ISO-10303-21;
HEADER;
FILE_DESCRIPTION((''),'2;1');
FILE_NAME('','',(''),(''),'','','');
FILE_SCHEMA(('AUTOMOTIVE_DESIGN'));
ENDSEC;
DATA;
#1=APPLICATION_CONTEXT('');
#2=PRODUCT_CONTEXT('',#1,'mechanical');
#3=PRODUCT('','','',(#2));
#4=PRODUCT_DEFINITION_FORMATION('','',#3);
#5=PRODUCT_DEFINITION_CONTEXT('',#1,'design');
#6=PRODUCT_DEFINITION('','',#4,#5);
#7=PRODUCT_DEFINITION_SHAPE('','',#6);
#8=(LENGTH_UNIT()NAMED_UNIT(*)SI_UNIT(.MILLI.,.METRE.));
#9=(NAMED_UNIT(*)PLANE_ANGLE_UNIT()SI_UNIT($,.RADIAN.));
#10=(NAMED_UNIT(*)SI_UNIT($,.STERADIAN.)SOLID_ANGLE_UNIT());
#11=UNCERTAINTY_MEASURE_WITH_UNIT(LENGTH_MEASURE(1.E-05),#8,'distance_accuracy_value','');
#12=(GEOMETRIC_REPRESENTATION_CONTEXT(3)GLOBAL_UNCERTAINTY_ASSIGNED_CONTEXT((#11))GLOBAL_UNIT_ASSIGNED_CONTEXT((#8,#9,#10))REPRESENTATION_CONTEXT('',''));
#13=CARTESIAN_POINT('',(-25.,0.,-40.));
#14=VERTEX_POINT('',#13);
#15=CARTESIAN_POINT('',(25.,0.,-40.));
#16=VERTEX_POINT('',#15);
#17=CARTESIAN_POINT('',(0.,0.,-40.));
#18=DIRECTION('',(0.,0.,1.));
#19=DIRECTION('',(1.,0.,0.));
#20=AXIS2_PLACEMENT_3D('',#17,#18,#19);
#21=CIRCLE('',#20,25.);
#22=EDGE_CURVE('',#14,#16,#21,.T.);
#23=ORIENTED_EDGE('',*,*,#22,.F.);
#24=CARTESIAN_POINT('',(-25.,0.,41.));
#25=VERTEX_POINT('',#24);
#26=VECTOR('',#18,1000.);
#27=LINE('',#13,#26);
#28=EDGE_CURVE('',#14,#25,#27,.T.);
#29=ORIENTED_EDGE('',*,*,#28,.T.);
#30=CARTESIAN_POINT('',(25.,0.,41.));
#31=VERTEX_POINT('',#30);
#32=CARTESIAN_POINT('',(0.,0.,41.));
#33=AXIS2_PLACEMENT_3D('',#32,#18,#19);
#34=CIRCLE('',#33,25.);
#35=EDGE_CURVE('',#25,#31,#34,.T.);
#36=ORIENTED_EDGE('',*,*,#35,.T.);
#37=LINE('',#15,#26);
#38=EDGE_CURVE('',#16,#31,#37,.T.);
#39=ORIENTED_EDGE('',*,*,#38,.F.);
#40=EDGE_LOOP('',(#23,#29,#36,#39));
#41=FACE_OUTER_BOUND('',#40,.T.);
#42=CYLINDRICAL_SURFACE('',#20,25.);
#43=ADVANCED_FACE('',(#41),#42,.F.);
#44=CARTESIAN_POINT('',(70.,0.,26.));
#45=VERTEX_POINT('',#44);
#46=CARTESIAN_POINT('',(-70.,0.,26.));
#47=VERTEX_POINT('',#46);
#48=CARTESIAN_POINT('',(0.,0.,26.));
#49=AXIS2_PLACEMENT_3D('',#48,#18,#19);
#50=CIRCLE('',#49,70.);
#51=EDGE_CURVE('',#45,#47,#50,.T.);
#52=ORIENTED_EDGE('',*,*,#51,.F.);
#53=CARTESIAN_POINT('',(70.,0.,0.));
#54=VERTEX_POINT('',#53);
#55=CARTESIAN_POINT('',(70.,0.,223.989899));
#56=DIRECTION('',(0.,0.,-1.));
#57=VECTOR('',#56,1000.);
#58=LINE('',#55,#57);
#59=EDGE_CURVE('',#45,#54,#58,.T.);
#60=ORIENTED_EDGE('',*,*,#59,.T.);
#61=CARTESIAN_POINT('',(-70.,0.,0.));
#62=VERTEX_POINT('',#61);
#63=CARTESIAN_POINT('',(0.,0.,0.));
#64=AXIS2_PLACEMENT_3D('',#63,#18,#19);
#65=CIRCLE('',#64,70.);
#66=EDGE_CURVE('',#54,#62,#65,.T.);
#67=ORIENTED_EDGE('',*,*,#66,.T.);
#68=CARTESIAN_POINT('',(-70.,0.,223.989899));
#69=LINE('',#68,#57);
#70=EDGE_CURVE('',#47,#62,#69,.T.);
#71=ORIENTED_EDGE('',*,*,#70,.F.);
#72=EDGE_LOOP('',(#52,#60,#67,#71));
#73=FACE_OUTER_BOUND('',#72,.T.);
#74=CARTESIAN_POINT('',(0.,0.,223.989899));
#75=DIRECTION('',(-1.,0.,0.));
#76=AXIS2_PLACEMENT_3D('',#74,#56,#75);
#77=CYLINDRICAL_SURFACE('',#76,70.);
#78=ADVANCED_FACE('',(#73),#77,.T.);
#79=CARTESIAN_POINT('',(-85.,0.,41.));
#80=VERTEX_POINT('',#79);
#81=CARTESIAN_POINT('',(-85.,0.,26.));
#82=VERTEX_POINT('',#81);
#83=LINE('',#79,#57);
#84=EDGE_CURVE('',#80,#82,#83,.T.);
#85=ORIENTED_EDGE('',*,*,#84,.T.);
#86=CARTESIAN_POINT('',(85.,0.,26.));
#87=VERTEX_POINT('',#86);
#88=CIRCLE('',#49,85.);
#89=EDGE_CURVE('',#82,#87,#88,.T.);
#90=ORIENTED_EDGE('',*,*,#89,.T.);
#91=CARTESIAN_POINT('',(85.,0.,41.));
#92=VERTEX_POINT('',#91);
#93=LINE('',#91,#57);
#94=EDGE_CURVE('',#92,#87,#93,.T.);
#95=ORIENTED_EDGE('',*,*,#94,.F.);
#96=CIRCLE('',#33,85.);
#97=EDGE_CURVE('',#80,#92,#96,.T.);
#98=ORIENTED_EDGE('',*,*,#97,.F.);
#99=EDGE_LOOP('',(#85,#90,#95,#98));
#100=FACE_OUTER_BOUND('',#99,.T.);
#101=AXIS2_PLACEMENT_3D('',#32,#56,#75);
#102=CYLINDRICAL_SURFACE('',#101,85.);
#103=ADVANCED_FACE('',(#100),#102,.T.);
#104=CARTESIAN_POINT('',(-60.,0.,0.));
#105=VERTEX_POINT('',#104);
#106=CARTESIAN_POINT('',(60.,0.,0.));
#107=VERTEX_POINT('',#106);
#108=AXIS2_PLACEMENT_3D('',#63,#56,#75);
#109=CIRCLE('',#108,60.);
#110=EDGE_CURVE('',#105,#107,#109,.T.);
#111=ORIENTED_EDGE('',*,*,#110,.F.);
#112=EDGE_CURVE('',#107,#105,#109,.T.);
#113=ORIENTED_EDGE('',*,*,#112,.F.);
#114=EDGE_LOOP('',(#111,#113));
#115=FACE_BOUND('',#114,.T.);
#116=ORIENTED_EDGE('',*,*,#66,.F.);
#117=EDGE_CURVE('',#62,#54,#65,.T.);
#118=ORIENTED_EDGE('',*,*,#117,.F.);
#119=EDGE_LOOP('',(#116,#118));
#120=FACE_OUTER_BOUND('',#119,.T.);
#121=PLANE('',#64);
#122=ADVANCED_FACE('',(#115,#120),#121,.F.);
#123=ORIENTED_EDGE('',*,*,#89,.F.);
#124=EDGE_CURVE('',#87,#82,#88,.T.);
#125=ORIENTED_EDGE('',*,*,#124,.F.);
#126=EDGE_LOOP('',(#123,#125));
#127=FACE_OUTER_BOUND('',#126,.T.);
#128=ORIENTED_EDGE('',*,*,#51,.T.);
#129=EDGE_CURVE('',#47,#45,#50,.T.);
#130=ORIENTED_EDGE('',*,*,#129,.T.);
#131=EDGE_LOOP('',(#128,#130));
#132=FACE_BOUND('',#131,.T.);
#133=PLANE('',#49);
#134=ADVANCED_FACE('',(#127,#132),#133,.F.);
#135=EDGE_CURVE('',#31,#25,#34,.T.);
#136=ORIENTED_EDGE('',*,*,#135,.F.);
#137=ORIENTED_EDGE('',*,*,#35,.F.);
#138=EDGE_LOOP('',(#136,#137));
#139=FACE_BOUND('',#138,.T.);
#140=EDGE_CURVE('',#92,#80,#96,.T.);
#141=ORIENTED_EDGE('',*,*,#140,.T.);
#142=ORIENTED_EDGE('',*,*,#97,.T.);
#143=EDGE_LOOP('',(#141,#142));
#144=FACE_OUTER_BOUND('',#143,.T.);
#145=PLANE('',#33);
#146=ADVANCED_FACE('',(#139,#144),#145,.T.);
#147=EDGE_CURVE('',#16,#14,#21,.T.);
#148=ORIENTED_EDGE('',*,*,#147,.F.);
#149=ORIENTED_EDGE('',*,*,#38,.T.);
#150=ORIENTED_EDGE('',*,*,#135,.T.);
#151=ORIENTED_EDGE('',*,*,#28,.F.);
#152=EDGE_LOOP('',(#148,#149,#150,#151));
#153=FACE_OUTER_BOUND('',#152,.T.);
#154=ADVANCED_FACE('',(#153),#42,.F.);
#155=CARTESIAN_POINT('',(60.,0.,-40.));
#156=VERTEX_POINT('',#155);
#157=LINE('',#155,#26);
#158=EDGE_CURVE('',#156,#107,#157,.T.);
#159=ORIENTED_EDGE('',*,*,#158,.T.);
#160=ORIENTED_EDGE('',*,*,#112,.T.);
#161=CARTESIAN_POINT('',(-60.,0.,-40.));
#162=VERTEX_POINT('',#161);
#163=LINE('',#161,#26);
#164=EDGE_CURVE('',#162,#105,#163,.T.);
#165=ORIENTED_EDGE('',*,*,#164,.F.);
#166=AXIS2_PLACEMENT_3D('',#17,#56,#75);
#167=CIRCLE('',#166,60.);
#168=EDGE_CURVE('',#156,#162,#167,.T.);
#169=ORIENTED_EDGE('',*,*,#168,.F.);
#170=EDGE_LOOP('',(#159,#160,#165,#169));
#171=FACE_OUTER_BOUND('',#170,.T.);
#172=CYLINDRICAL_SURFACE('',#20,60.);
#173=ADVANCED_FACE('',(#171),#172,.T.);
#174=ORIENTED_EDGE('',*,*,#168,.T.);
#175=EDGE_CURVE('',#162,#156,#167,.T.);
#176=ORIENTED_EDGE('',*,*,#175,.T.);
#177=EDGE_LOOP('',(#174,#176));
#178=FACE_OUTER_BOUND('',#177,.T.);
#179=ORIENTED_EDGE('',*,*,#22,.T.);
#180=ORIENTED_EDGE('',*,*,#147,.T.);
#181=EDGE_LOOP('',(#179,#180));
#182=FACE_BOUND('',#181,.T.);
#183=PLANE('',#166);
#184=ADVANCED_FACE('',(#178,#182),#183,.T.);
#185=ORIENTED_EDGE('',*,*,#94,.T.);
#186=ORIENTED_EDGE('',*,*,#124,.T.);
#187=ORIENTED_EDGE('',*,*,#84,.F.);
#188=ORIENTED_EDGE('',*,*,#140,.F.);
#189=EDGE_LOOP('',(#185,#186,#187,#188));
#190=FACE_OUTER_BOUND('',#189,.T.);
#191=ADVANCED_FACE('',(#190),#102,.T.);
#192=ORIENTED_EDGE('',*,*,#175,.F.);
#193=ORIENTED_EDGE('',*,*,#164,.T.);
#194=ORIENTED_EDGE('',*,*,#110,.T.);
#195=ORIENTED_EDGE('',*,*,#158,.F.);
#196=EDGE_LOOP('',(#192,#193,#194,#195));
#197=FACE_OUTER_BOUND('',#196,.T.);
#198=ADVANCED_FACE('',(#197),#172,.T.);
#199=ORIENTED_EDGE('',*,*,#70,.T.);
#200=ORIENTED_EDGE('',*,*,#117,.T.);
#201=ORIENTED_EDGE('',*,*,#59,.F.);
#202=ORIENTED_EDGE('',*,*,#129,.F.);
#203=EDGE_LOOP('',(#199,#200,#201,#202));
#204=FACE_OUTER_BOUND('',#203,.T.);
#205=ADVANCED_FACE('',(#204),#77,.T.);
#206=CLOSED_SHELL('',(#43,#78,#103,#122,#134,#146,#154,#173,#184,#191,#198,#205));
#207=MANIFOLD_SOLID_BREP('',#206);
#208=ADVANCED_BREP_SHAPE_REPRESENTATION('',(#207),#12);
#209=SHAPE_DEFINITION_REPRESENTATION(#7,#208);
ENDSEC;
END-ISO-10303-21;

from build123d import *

# Parameters (mm, degrees)
SKETCH1_R               = 70
BOSS_EXTRUDE1_DEPTH     = 26
SKETCH2_R               = 85
BOSS_EXTRUDE2_DEPTH     = 15
SKETCH3_R               = 60
BOSS_EXTRUDE3_DEPTH     = 40
CUT_EXTRUDE1_DEPTH      = 145.951716099
CUT_EXTRUDE1_DEPTH_BACK = 145.951716099
SKETCH4_R               = 25


with BuildPart() as part:
    # Sketch1 → Boss-Extrude1 (new body)
    with BuildSketch(Plane.XY):
        Circle(SKETCH1_R)
    extrude(amount=BOSS_EXTRUDE1_DEPTH)

    # Sketch2 → Boss-Extrude2 (add)
    with BuildSketch(Plane.XY.offset(26)):
        Circle(SKETCH2_R)
    extrude(amount=BOSS_EXTRUDE2_DEPTH)

    # Sketch3 → Boss-Extrude3 (add)
    with BuildSketch(Plane(origin=(0, 0, 0), x_dir=(-1, 0, 0), z_dir=(0, 0, -1))):
        Circle(SKETCH3_R)
    extrude(amount=BOSS_EXTRUDE3_DEPTH)

    # Sketch4 → Cut-Extrude1 (cut, two sides: drawn at the far end of the back side and taken through both)
    with BuildSketch(Plane.XY.offset(41).offset(-CUT_EXTRUDE1_DEPTH_BACK)):
        Circle(SKETCH4_R)
    extrude(amount=CUT_EXTRUDE1_DEPTH + CUT_EXTRUDE1_DEPTH_BACK, mode=Mode.SUBTRACT)


solid = part.part
